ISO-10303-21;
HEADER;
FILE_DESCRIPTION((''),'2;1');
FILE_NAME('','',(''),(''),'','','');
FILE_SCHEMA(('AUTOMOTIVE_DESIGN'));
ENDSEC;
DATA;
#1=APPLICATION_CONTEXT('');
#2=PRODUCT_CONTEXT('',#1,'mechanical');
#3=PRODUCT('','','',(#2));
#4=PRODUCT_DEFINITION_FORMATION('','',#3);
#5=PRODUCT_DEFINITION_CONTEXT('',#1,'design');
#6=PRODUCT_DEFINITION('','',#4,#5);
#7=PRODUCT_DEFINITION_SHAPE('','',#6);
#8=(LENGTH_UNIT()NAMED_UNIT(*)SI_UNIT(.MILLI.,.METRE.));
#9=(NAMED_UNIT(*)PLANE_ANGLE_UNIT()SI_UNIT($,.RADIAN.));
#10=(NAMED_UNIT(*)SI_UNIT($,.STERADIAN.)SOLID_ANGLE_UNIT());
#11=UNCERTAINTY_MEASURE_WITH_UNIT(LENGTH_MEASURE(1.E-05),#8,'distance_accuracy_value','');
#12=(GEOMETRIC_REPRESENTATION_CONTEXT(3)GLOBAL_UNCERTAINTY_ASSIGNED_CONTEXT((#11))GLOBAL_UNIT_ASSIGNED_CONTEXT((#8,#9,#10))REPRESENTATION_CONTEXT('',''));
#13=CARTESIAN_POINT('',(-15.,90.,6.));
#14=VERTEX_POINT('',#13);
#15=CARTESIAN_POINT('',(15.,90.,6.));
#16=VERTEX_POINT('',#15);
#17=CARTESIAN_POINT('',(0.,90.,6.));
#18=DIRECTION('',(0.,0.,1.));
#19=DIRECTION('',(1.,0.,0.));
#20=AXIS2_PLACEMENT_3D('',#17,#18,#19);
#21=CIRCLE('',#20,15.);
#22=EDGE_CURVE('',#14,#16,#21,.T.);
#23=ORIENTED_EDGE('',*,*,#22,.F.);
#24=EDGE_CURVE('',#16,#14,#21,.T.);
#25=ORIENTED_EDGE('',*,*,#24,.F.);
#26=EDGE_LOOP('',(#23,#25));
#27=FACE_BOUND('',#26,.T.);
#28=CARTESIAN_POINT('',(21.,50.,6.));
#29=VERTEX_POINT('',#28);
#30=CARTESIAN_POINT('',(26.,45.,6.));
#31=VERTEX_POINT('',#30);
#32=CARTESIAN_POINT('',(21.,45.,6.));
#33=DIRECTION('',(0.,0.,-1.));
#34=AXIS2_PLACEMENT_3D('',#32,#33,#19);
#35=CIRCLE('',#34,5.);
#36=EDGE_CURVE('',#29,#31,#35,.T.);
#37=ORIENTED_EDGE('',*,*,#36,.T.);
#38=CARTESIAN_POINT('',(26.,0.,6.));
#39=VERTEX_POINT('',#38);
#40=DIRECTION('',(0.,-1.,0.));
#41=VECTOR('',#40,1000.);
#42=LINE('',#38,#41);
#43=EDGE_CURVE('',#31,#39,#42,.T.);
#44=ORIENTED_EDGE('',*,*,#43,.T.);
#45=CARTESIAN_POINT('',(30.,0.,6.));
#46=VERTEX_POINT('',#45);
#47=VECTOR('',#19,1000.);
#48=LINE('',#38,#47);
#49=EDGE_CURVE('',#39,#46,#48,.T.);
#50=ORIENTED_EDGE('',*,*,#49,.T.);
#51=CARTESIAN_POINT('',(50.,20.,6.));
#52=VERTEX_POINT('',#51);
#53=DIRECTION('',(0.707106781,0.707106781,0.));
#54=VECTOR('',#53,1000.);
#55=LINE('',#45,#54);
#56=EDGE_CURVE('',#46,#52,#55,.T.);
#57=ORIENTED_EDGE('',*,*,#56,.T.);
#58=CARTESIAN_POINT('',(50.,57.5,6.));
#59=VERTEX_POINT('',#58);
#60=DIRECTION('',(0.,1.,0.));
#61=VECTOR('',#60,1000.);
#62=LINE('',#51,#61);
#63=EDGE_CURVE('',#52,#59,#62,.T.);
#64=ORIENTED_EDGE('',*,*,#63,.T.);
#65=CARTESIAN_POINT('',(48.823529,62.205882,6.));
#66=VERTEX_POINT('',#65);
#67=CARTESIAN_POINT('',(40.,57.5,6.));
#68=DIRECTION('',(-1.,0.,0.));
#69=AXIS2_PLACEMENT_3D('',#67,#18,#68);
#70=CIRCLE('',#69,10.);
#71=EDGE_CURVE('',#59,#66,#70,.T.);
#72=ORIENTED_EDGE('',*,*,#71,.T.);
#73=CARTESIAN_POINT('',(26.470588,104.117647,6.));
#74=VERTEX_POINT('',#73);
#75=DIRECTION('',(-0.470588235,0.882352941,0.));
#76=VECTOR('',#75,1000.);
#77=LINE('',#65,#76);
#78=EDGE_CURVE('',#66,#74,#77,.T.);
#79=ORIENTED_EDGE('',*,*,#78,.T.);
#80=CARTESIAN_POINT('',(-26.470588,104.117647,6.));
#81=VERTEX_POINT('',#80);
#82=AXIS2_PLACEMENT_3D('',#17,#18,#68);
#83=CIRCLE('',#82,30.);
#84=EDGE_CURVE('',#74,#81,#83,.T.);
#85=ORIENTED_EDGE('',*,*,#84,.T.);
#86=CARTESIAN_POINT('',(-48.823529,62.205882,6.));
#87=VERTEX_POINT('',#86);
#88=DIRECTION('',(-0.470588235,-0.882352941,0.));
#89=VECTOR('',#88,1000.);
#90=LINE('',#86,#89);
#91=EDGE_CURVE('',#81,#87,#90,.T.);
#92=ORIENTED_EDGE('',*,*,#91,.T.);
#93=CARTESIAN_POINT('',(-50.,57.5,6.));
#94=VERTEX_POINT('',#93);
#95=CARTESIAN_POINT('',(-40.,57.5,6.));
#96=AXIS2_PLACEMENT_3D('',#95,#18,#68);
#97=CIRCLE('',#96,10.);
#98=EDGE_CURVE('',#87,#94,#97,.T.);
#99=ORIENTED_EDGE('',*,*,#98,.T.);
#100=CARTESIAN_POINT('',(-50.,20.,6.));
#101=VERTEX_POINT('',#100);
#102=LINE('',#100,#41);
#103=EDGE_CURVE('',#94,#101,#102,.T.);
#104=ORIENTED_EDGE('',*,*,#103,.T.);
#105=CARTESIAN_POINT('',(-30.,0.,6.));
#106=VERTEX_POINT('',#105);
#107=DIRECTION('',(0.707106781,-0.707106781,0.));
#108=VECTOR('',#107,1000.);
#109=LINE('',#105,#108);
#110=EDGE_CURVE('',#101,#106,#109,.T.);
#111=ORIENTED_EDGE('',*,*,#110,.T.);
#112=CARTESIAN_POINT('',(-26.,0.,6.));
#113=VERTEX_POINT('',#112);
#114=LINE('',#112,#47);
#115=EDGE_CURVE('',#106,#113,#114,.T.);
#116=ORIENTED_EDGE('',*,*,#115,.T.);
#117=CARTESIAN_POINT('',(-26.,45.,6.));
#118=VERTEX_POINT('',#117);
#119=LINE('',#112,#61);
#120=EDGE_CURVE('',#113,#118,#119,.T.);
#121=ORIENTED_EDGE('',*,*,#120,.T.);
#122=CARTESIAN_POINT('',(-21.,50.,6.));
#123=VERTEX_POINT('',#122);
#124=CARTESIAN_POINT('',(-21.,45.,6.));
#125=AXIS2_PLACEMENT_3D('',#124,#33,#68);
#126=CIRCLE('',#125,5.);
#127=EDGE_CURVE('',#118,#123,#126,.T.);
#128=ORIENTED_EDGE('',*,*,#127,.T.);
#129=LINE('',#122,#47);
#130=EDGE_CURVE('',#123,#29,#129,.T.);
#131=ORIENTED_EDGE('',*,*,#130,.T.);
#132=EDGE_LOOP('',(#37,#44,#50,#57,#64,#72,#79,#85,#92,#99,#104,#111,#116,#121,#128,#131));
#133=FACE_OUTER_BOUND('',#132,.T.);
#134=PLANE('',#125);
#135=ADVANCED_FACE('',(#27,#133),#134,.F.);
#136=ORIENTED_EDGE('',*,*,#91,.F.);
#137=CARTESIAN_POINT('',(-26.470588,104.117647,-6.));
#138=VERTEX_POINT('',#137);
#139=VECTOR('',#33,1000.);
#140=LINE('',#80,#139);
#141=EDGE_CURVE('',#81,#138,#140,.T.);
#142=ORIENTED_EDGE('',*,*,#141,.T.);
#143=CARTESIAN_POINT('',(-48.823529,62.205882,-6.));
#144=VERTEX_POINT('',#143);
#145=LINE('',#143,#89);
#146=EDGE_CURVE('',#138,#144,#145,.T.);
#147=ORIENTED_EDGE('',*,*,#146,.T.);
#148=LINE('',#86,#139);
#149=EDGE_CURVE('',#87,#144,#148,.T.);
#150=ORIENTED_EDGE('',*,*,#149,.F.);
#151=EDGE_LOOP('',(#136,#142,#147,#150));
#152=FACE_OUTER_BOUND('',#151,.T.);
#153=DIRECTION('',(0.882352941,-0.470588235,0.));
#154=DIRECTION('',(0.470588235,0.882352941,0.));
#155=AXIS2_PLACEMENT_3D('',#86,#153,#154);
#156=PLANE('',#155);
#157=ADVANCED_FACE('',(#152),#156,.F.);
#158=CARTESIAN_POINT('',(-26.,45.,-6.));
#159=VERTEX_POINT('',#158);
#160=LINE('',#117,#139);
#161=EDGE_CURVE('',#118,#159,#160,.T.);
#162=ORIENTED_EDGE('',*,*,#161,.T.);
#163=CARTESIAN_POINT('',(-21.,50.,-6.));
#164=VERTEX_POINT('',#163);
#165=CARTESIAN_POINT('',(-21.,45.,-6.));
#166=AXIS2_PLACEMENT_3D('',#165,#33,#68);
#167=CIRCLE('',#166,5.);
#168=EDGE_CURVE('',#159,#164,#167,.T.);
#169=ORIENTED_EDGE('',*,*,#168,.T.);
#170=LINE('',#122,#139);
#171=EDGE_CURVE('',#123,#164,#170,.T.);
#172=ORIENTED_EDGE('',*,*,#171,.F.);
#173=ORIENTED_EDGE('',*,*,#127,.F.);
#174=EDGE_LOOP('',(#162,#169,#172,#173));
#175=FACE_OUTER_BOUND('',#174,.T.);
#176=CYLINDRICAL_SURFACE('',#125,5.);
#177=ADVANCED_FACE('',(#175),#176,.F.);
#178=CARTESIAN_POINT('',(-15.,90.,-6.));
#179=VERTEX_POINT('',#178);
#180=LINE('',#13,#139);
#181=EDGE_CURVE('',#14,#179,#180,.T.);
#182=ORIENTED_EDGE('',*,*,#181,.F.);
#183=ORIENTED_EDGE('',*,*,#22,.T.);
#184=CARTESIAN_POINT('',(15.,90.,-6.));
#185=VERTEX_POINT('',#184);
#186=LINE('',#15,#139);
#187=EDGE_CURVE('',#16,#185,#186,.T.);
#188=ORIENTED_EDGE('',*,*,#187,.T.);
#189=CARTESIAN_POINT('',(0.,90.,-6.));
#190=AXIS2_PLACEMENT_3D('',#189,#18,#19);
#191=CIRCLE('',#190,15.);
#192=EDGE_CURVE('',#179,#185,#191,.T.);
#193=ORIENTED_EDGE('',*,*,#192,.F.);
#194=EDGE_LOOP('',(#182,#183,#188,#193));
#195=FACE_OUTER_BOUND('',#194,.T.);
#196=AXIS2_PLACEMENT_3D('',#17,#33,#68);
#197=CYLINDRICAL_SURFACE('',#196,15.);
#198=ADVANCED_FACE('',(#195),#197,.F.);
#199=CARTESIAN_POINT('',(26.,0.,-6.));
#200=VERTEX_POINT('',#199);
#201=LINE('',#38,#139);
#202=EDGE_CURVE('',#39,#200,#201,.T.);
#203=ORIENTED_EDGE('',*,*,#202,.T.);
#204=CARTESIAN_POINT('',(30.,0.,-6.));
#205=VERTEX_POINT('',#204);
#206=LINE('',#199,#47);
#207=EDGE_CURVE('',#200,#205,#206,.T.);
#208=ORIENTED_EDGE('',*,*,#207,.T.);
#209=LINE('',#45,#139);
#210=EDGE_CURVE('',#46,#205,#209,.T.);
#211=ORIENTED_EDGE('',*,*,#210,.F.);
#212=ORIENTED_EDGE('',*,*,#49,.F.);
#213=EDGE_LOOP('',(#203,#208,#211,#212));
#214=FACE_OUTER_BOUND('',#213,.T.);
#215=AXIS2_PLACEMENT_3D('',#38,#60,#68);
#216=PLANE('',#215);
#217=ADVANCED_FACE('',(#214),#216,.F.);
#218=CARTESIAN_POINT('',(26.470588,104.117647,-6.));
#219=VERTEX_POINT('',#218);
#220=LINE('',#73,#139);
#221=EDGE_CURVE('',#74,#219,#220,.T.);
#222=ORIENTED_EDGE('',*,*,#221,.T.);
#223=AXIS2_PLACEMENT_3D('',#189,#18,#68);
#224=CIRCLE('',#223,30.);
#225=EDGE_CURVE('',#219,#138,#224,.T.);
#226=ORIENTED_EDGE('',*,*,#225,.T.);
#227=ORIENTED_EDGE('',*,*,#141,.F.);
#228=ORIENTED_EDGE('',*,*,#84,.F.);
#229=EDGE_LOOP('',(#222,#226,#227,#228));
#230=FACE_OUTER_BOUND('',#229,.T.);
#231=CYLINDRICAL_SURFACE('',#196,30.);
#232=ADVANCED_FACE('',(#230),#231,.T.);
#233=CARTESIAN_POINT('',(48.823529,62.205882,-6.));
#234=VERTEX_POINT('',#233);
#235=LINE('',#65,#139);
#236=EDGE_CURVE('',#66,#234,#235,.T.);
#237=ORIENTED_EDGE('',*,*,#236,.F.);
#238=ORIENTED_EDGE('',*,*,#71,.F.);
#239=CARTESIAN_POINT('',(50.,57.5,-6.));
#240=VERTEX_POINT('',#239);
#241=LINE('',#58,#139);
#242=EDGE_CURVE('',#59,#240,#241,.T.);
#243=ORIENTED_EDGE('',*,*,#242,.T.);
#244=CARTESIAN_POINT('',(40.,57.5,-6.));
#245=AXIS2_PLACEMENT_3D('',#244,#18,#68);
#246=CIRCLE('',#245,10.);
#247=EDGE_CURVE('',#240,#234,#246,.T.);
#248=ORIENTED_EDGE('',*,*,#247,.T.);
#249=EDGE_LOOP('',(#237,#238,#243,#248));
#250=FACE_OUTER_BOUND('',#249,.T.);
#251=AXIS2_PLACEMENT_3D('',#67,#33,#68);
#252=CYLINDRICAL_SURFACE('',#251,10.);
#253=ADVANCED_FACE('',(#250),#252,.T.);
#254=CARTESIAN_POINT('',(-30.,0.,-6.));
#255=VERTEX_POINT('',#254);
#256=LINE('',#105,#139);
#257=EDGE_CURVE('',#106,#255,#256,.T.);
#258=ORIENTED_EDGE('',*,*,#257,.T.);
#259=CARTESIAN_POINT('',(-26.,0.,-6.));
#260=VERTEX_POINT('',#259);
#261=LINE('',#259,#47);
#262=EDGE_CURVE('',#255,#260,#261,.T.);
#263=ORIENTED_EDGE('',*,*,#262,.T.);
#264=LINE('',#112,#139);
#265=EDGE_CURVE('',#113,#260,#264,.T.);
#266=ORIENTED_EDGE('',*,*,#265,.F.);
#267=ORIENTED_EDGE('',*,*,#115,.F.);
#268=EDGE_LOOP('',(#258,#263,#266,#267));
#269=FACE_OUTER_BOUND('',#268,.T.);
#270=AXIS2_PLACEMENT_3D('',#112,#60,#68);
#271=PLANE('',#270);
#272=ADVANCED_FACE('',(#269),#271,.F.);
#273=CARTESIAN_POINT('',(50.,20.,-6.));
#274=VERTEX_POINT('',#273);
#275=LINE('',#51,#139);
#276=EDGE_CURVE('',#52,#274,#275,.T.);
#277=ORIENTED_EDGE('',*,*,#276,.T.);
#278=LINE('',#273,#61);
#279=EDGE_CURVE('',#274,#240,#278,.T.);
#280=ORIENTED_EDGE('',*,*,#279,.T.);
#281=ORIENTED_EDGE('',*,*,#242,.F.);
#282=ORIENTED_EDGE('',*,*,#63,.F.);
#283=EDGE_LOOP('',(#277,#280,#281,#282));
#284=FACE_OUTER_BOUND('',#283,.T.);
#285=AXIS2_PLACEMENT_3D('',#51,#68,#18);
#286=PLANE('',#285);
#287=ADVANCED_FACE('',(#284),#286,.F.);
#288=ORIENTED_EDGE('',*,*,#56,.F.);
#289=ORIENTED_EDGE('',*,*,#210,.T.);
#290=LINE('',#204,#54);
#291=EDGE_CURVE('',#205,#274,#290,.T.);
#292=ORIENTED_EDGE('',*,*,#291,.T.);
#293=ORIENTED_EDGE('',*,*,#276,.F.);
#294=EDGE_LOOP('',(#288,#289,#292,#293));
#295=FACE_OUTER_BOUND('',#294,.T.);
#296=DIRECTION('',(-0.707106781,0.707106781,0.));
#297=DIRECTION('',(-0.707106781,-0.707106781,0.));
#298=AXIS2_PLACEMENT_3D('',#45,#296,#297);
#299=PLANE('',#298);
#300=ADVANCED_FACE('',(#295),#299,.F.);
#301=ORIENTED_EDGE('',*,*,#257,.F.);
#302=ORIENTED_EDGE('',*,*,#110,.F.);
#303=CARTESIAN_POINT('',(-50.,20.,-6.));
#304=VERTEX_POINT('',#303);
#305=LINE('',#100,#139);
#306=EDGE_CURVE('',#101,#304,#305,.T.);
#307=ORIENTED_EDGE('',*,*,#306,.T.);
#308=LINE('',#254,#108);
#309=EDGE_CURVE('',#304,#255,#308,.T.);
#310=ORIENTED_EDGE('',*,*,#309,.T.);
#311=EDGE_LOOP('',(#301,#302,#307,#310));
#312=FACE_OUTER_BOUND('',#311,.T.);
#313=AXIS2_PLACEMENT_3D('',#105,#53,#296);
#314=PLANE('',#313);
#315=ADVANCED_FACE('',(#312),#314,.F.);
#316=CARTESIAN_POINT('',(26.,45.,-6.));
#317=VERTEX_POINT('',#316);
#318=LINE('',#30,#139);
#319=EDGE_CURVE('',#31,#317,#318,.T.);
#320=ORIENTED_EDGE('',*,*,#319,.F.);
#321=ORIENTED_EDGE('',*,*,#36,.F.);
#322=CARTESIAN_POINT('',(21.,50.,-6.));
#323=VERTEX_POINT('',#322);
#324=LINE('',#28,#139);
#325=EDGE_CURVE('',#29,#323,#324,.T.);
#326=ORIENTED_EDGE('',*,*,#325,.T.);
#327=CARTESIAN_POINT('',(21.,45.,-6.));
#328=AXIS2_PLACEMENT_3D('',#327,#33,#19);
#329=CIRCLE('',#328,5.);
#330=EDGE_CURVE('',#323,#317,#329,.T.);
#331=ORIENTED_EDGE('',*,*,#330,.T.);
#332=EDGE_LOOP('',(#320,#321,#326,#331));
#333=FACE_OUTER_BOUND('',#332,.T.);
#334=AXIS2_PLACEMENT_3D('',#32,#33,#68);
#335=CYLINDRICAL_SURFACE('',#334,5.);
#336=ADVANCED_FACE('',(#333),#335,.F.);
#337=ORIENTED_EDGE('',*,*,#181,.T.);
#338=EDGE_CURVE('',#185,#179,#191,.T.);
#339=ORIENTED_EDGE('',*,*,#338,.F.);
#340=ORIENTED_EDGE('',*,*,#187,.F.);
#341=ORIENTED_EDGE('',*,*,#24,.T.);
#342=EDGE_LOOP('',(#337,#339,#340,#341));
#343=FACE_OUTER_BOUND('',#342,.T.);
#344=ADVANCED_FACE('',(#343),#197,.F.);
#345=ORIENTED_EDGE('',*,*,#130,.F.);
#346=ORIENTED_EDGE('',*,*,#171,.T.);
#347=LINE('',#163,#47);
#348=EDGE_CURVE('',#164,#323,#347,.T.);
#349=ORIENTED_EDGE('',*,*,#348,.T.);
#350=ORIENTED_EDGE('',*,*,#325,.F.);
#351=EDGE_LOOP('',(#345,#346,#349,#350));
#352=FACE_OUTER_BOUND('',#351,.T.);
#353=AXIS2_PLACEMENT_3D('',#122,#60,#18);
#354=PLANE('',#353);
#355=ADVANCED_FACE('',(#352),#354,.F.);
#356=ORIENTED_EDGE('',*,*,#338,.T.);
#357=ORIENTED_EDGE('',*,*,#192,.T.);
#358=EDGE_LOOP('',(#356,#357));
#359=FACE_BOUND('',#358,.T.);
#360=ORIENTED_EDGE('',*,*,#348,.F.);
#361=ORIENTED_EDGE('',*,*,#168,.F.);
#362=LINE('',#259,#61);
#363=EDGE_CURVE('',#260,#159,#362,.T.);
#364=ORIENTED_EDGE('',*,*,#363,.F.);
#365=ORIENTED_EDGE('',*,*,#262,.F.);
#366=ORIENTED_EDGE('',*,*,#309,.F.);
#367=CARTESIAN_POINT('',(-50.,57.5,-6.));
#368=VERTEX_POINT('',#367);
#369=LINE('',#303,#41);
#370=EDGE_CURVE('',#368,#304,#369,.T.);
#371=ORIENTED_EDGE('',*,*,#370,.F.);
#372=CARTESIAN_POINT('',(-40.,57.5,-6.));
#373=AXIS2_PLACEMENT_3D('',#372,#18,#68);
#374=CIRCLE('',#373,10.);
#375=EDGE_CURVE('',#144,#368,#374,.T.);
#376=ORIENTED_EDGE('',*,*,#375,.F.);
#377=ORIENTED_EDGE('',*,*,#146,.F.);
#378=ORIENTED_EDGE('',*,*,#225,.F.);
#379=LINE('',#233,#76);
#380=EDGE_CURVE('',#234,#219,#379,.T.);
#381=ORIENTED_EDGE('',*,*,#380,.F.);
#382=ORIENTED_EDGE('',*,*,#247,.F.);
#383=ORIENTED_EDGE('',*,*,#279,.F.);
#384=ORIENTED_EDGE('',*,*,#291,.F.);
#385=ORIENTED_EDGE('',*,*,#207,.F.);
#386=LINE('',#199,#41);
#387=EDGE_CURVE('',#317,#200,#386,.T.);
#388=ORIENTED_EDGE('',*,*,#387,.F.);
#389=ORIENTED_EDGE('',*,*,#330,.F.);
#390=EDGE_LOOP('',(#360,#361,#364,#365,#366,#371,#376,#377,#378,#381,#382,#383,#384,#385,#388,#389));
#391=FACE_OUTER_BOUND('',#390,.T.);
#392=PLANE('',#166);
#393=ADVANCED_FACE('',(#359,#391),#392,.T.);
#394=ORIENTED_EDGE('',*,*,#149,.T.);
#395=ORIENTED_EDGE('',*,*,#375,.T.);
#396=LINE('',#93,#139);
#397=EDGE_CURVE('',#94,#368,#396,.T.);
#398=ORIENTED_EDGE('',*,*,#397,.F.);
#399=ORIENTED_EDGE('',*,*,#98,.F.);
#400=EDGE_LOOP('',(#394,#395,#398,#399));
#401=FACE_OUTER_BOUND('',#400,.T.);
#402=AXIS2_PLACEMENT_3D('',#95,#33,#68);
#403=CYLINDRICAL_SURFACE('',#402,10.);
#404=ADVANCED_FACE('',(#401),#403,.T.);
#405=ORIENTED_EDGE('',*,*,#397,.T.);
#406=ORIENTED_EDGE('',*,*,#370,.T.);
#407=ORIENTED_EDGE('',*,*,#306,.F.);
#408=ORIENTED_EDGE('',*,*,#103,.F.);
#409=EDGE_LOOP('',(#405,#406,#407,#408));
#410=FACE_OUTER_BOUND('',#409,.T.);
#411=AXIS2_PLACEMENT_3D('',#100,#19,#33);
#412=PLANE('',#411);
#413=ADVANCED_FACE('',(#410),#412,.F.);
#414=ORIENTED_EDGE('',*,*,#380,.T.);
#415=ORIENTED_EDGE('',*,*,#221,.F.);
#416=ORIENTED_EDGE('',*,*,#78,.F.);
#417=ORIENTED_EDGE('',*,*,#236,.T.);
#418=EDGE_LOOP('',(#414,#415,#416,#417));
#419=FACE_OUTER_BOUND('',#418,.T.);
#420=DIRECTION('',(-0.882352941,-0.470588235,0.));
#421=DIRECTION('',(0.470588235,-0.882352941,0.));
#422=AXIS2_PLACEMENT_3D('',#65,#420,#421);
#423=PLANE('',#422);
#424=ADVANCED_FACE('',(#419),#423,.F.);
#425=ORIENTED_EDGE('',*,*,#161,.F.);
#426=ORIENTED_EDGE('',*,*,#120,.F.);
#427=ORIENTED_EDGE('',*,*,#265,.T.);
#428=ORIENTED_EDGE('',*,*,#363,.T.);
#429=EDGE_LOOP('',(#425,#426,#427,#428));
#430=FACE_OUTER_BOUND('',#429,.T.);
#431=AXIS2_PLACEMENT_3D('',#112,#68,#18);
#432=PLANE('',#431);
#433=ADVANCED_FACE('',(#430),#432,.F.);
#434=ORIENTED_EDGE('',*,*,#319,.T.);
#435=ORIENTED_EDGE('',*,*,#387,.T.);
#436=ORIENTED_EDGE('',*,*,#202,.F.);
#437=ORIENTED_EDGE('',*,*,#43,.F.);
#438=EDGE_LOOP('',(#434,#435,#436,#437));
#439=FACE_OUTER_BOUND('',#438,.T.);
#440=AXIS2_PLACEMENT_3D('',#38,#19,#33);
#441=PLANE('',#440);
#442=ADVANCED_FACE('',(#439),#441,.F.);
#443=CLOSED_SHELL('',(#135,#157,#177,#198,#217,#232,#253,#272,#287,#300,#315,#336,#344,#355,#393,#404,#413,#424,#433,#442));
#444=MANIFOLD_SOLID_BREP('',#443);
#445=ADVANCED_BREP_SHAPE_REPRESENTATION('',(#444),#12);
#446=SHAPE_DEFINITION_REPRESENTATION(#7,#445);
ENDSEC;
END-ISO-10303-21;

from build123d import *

# Parameters (mm, degrees)
SKETCH1_R           = 15
BOSS_EXTRUDE1_DEPTH = 6


with BuildPart() as part:
    # Sketch1 → Boss-Extrude1 (new, symmetric)
    with BuildSketch(Plane.XY):
        with BuildLine():
            Line((-26, 0), (-30, 0))
            Line((-30, 0), (-50, 20))
            Line((-50, 20), (-50, 57.5))
            ThreePointArc((-50, 57.5), (-49.701425001, 59.92535625), (-48.823529412, 62.205882353))
            Line((-48.823529412, 62.205882353), (-26.470588235, 104.117647059))
            ThreePointArc((-26.470588235, 104.117647059), (0, 120), (26.470588235, 104.117647059))
            Line((26.470588235, 104.117647059), (48.823529412, 62.205882353))
            ThreePointArc((48.823529412, 62.205882353), (49.701425001, 59.92535625), (50, 57.5))
            Line((50, 57.5), (50, 20))
            Line((50, 20), (30, 0))
            Line((30, 0), (26, 0))
            Line((26, 0), (26, 45))
            ThreePointArc((26, 45), (24.535533906, 48.535533906), (21, 50))
            Line((21, 50), (-21, 50))
            ThreePointArc((-21, 50), (-24.535533906, 48.535533906), (-26, 45))
            Line((-26, 45), (-26, 0))
        make_face()
        with Locations((0, 90)):
            Circle(SKETCH1_R, mode=Mode.SUBTRACT)
    extrude(amount=BOSS_EXTRUDE1_DEPTH, both=True)


solid = part.part
